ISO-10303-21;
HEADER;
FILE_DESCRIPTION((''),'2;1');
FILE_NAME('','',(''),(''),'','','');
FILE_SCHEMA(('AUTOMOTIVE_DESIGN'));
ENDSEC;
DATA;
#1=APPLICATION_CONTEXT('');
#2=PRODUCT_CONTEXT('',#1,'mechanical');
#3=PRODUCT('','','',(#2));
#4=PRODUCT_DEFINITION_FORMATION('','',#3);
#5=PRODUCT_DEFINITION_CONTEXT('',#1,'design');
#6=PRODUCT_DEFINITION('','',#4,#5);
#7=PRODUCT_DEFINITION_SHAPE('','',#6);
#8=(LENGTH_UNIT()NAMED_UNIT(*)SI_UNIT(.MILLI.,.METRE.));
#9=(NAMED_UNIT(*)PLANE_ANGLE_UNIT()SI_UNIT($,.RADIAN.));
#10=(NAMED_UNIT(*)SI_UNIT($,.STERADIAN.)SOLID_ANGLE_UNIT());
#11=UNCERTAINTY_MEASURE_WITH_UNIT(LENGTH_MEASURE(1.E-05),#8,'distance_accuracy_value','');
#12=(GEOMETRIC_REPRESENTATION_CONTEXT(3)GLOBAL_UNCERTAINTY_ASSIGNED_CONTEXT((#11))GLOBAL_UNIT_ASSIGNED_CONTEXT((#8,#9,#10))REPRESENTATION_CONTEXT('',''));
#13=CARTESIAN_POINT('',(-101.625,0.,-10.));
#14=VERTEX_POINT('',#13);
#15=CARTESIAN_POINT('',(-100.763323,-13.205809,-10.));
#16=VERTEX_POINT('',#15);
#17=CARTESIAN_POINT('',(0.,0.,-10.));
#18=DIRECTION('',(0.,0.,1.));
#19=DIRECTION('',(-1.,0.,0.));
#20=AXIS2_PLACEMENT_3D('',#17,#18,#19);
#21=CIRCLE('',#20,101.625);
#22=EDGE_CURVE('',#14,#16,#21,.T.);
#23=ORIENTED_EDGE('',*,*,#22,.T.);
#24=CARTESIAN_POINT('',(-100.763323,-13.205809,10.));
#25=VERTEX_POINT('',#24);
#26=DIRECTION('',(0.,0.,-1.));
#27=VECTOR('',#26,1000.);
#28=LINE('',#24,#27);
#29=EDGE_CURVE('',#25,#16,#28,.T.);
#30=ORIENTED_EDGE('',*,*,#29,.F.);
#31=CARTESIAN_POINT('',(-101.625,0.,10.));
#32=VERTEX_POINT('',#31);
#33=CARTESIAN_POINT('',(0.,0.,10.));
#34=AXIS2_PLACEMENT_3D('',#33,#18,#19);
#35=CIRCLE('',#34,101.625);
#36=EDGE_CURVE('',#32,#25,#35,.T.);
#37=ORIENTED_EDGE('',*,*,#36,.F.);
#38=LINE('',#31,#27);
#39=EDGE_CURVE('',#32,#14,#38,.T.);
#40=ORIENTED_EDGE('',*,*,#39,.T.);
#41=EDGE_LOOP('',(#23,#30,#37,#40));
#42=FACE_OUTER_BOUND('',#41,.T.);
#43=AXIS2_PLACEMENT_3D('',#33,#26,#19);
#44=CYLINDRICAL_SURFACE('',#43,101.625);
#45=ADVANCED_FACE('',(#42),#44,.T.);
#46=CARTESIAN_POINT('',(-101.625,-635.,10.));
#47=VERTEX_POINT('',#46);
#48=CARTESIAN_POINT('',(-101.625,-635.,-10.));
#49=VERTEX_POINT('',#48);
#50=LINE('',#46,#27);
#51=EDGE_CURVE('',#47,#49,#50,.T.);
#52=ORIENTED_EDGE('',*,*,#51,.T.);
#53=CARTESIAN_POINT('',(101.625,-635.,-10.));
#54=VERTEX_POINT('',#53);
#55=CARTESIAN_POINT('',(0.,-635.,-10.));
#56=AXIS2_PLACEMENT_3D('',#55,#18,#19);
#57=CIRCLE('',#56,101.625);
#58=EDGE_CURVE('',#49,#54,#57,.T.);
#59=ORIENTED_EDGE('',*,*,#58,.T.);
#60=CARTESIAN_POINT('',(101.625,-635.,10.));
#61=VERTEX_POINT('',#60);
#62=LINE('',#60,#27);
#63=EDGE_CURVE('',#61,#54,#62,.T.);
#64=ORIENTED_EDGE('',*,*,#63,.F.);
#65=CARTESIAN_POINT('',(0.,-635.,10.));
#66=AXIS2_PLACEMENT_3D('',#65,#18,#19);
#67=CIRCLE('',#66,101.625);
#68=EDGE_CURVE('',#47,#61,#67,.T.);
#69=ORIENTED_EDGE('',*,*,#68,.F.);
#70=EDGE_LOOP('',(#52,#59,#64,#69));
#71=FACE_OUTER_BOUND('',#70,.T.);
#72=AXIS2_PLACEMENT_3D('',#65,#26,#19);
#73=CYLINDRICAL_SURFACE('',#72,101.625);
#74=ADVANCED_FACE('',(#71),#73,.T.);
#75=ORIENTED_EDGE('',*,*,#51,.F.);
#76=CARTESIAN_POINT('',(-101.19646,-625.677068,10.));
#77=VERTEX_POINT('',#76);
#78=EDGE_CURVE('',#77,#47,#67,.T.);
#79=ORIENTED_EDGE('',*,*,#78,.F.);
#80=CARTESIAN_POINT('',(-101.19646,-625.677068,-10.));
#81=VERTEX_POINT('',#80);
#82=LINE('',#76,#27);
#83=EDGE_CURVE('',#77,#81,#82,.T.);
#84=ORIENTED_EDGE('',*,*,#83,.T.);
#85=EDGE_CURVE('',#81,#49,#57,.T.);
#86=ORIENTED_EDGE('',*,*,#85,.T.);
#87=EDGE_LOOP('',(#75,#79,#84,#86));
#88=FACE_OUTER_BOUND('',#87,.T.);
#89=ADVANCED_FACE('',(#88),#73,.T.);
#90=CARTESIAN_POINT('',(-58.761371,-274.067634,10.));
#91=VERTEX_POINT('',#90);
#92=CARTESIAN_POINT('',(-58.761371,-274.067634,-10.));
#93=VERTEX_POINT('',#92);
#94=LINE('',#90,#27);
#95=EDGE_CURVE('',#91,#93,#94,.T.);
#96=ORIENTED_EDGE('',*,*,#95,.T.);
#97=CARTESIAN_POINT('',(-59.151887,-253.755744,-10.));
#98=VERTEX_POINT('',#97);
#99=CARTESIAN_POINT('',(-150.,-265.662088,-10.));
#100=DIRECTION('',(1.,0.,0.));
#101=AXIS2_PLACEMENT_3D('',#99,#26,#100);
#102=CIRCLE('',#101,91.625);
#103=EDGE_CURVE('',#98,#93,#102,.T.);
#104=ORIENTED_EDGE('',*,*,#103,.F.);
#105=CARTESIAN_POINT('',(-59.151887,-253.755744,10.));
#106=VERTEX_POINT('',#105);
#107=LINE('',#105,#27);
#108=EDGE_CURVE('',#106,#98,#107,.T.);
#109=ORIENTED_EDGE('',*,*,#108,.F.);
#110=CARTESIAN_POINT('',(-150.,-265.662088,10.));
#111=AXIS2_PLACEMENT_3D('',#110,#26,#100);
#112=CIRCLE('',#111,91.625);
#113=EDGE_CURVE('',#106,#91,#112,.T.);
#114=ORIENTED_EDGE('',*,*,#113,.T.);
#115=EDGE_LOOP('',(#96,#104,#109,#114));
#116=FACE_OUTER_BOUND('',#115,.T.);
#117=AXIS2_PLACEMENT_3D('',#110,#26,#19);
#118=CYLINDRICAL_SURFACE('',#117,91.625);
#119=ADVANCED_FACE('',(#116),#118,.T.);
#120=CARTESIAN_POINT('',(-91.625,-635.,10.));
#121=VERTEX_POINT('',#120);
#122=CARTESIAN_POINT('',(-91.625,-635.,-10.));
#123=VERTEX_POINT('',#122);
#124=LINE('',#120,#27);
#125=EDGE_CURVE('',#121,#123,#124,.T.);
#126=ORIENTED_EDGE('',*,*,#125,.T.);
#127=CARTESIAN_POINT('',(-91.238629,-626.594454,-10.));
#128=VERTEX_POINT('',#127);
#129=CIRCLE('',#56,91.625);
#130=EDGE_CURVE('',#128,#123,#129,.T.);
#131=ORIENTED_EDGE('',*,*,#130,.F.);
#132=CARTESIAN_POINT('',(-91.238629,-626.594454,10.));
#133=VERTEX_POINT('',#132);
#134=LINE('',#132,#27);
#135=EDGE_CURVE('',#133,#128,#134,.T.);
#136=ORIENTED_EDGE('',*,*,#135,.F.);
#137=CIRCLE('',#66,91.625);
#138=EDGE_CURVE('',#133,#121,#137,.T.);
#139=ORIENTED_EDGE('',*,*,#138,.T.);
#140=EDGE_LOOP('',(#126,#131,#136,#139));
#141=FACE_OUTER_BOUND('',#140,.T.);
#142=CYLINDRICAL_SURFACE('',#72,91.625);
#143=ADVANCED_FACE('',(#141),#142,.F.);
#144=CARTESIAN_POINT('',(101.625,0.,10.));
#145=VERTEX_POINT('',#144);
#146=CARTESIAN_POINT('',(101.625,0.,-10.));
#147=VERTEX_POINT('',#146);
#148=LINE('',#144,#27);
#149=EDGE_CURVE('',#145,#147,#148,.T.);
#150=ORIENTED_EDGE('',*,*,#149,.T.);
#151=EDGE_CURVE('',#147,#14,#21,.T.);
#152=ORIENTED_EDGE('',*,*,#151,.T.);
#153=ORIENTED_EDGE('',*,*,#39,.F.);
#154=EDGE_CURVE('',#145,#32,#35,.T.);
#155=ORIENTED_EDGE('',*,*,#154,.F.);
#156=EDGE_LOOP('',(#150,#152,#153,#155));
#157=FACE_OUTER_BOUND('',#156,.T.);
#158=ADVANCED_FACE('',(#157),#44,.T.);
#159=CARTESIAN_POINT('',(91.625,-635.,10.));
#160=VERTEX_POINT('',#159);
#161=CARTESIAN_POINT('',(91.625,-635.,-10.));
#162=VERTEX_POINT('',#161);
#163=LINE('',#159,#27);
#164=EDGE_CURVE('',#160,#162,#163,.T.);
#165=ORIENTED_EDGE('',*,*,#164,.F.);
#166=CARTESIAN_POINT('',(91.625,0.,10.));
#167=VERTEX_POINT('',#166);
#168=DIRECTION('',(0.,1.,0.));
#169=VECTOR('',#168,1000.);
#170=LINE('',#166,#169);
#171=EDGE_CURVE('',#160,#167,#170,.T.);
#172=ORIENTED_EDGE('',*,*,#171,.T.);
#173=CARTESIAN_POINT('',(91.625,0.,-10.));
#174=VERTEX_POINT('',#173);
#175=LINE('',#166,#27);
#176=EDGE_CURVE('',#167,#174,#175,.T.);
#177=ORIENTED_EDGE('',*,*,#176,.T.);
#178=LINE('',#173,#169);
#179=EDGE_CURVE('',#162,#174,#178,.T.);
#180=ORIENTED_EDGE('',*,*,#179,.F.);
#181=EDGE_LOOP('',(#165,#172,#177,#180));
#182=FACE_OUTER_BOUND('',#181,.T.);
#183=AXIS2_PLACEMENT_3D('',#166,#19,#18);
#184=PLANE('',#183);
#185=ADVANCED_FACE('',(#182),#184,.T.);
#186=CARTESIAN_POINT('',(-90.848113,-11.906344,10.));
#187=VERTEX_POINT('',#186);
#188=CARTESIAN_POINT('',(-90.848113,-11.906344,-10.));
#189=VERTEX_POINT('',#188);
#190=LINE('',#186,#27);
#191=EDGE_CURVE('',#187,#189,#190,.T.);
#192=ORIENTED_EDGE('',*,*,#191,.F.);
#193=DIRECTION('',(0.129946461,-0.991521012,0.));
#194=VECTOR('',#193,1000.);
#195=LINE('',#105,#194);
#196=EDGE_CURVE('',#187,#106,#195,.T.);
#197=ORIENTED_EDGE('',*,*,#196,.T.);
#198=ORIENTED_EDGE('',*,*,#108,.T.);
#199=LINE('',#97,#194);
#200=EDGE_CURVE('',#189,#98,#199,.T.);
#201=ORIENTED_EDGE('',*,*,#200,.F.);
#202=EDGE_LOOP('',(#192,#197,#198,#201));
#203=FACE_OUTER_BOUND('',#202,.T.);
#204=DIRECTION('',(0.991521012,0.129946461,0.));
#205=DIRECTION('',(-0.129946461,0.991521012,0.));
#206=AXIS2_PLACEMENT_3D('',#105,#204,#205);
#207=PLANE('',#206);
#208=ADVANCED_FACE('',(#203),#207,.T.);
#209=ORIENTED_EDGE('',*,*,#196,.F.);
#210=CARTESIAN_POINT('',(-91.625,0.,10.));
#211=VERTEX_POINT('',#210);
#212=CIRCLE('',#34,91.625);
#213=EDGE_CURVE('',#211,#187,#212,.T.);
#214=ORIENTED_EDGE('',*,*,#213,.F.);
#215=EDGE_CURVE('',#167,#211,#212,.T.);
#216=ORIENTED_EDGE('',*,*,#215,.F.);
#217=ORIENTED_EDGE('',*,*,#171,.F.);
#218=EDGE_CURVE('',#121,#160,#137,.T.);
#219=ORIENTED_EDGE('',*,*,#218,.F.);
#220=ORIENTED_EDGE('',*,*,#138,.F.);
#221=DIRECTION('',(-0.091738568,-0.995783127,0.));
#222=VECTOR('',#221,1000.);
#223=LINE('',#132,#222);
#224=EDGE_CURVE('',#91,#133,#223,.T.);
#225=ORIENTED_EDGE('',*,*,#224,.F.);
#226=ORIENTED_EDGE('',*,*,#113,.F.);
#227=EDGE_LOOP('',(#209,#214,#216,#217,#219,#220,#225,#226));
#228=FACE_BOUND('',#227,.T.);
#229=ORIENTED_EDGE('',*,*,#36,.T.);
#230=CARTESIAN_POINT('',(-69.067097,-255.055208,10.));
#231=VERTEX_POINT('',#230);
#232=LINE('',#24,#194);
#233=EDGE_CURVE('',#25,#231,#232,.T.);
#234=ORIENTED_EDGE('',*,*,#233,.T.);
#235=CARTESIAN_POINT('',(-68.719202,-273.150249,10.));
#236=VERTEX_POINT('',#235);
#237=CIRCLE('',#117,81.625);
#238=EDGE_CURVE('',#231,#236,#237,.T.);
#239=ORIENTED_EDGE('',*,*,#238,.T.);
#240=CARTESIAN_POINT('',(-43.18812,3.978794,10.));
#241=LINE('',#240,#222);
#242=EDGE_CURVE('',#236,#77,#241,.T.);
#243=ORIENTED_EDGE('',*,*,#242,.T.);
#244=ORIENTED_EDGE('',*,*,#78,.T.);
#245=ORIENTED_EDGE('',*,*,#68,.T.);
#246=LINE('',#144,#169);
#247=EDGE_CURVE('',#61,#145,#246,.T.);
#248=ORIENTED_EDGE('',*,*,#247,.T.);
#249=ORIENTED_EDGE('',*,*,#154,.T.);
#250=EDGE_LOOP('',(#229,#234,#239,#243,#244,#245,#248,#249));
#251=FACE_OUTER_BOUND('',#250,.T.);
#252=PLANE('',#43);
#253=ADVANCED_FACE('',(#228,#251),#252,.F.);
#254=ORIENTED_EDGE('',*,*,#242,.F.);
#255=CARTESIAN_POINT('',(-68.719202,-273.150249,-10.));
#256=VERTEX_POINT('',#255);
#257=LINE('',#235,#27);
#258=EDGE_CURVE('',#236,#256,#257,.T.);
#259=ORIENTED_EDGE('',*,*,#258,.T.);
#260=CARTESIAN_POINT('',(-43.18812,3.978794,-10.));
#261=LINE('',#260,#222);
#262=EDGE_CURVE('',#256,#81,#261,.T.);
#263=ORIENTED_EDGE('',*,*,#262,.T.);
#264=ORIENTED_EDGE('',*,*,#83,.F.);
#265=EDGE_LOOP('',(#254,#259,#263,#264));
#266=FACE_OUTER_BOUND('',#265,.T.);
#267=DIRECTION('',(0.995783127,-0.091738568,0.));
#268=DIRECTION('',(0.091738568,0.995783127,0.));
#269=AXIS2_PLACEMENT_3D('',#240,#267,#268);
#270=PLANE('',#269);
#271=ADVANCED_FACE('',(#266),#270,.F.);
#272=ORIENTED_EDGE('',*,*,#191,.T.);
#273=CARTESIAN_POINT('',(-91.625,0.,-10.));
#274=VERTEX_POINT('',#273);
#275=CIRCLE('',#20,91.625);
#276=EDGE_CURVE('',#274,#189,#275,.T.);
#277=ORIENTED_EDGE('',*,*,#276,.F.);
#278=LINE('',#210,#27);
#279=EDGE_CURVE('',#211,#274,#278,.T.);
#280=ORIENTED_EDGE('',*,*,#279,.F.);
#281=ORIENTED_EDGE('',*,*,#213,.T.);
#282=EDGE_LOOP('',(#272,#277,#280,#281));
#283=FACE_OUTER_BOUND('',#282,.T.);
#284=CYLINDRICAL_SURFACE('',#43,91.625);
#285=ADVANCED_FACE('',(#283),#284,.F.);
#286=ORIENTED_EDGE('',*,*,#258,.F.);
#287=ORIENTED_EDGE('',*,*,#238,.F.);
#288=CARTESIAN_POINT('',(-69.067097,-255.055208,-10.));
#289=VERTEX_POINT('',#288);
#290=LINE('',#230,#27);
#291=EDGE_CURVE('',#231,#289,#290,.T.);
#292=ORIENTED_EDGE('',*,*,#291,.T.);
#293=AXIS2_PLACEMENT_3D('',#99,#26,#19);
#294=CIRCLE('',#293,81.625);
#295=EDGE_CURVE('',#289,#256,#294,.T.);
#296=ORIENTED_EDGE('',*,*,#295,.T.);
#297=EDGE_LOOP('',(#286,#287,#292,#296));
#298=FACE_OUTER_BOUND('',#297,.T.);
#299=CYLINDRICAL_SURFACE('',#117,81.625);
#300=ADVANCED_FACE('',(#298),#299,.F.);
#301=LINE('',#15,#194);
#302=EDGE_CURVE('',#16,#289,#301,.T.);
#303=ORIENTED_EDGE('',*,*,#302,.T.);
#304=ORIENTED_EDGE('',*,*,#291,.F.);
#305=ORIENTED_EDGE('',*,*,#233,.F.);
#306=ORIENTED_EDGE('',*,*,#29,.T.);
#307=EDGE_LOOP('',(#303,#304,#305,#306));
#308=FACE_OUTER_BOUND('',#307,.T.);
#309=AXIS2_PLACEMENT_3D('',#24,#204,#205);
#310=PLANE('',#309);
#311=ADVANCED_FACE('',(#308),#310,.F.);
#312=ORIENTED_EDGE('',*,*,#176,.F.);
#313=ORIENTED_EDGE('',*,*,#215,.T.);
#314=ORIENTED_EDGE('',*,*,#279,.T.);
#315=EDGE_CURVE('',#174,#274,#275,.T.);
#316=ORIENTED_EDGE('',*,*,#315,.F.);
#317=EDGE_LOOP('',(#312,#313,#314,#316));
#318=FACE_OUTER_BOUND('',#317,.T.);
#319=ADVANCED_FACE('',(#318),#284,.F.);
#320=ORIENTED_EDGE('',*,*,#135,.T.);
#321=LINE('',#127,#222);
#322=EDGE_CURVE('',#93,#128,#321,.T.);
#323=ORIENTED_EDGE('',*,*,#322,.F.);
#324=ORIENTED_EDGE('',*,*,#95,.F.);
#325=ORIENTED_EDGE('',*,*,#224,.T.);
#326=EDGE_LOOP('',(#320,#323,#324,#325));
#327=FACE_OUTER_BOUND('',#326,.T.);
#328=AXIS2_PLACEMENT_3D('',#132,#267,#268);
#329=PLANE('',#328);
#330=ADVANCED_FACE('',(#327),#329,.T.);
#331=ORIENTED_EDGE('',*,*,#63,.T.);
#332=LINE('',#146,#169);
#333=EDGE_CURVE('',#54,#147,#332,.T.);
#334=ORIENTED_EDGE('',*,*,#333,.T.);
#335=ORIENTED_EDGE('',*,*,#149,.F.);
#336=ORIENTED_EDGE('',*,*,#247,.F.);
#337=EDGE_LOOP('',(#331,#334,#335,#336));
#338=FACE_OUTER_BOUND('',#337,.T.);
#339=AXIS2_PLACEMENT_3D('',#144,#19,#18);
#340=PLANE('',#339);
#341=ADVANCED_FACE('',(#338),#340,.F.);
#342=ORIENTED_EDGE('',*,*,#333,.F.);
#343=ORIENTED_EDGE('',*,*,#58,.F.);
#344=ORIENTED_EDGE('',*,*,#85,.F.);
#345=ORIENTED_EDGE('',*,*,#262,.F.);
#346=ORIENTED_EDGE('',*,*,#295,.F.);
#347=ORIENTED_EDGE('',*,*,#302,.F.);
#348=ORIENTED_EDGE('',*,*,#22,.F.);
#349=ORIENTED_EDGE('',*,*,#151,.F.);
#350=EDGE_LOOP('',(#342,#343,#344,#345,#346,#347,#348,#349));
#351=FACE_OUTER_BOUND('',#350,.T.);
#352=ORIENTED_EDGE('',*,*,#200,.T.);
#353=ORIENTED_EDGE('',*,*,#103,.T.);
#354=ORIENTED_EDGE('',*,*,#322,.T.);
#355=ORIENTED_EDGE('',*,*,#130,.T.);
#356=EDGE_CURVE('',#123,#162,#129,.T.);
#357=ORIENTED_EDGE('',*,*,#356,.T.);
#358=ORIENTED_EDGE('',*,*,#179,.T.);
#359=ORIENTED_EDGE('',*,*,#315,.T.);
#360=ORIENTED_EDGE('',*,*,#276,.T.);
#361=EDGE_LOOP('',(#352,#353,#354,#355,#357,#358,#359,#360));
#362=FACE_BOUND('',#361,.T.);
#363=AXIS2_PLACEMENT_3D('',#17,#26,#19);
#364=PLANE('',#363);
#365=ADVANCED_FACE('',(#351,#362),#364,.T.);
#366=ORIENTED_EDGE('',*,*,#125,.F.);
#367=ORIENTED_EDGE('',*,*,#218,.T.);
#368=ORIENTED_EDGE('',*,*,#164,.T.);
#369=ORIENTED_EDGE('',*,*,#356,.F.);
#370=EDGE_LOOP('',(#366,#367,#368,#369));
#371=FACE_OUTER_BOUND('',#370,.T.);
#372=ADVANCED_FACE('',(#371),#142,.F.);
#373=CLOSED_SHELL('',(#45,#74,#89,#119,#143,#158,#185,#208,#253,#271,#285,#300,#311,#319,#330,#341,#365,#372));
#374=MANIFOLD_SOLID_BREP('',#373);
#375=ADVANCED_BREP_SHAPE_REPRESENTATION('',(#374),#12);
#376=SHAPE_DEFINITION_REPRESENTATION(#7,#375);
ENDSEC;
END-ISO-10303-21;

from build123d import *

# Parameters (mm, degrees)
EXTRUDE_1_DEPTH = 10


with BuildPart() as part:
    # 草图2 → 拉伸-薄壁1 (new, symmetric)
    with BuildSketch(Plane.XY):
        with BuildLine():
            Line((-69.067097429, -255.055208246), (-100.763322879, -13.205809086))
            ThreePointArc((-100.763322879, -13.205809085), (-6.616945736, 101.40935193), (101.624999966, 2.2e-08))
            Line((101.624999966, 2.2e-08), (101.624999966, -634.999999978))
            ThreePointArc((101.624999966, -634.999999978), (-4.66638799, -736.517808507), (-101.196460274, -625.677068041))
            Line((-101.196460274, -625.677068041), (-68.719202326, -273.150248716))
            ThreePointArc((-68.719202326, -273.150248716), (-68.390081735, -264.093056497), (-69.067097429, -255.055208246))
        make_face()
        with BuildLine():
            Line((-59.151887309, -253.755743635), (-90.848112759, -11.906344475))
            ThreePointArc((-90.848112759, -11.906344475), (-5.965831768, 91.430571914), (91.624999966, 2.2e-08))
            Line((91.624999966, 2.2e-08), (91.624999966, -634.999999978))
            ThreePointArc((91.624999966, -634.999999978), (-4.207210823, -726.528356253), (-91.238629008, -626.594453717))
            Line((-91.238629008, -626.594453717), (-58.76137106, -274.067634393))
            ThreePointArc((-58.76137106, -274.067634393), (-58.391929417, -263.900832101), (-59.151887309, -253.755743635))
        make_face(mode=Mode.SUBTRACT)
    extrude(amount=EXTRUDE_1_DEPTH, both=True)


solid = part.part
